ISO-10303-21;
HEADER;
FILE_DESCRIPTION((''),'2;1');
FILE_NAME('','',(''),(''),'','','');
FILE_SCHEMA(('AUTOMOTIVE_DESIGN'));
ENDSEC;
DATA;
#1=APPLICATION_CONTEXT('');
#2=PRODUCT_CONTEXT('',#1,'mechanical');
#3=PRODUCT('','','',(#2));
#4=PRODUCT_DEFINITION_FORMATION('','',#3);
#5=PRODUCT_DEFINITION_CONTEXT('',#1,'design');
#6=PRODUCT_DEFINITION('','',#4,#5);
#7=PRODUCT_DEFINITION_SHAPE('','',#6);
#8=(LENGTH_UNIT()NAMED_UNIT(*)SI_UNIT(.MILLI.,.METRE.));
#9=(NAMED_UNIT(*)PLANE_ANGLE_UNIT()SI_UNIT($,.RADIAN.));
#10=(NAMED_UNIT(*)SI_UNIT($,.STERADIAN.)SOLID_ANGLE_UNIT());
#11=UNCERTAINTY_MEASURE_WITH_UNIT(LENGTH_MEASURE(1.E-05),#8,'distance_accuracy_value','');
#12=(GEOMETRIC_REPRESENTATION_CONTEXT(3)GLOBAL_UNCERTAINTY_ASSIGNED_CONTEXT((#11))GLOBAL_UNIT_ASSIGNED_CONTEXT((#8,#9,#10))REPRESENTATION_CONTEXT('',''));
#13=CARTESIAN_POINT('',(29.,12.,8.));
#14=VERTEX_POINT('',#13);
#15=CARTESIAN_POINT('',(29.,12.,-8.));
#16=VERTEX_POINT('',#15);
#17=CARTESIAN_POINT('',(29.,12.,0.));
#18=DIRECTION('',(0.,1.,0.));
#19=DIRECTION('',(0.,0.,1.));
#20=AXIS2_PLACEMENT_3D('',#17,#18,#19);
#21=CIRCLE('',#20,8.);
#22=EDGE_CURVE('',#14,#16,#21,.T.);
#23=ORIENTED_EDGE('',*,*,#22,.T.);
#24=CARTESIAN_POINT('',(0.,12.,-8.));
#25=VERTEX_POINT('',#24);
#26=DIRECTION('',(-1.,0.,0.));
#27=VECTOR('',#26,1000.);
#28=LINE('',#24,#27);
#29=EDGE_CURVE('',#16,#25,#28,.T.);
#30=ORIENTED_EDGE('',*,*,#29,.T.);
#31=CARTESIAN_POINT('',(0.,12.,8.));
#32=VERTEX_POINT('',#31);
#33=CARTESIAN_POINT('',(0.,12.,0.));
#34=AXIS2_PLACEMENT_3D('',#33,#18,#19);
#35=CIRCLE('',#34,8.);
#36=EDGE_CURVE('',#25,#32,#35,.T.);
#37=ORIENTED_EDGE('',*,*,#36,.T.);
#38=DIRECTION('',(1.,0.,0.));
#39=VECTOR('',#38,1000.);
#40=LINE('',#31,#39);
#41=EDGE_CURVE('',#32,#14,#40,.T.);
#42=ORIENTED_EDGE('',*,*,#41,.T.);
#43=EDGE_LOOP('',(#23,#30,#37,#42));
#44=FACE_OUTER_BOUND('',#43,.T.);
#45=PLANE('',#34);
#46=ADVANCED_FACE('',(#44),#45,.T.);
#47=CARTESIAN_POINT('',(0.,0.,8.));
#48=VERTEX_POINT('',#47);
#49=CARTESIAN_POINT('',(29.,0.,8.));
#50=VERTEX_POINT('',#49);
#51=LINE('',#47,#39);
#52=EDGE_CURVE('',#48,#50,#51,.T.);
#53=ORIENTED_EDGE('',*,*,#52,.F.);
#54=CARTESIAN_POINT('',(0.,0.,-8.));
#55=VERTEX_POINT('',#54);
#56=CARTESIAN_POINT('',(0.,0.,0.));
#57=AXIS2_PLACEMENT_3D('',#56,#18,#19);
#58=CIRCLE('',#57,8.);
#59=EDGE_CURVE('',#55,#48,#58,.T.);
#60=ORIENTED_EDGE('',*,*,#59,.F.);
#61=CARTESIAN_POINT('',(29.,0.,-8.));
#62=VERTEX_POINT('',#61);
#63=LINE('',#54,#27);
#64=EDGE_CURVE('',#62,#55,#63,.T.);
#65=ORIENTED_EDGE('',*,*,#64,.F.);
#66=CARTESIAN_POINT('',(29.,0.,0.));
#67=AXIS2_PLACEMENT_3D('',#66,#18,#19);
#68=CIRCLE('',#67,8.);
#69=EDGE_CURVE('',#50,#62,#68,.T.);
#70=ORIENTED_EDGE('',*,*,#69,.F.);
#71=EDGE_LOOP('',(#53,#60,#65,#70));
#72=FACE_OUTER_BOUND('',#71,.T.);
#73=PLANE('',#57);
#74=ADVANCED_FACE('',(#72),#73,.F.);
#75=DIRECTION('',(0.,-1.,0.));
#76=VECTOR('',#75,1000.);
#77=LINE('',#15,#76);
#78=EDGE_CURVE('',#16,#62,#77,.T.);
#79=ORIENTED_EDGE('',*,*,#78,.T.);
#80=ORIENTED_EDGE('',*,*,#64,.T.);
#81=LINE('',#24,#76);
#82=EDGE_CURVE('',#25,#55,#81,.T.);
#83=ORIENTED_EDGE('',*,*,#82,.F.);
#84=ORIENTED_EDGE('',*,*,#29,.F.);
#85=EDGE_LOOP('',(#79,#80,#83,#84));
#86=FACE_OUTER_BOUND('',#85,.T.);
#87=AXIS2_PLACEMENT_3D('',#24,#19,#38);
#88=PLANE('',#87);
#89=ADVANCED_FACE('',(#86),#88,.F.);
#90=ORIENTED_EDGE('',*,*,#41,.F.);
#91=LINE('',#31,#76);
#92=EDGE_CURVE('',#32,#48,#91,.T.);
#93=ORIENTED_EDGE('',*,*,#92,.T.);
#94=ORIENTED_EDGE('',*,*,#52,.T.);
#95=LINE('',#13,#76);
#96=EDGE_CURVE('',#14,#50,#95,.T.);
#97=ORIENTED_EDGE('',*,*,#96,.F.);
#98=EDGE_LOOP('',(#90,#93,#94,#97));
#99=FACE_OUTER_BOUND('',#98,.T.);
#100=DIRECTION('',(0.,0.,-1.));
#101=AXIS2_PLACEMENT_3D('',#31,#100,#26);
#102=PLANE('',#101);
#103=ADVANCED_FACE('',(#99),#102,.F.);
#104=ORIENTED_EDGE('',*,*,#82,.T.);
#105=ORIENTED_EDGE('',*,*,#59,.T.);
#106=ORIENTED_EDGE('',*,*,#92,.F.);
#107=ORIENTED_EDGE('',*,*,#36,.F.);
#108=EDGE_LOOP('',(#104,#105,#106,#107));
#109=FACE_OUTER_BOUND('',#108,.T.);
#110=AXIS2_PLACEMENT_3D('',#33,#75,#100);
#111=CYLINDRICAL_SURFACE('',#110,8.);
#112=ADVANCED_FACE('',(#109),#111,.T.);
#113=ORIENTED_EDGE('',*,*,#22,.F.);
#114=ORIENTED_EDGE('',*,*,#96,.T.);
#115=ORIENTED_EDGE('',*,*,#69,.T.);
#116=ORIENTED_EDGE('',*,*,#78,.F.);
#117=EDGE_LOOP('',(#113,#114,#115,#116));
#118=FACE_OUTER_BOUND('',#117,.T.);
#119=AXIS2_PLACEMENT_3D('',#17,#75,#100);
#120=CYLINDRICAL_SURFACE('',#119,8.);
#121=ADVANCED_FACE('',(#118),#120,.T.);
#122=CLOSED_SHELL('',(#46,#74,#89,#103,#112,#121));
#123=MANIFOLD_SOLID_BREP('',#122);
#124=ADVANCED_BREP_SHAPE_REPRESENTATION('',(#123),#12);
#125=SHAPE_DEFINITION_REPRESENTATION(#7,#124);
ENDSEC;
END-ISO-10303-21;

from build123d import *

# Parameters (mm, degrees)
BOSS_EXTRUDE1_DEPTH = 12


with BuildPart() as part:
    # Sketch1 → Boss-Extrude1 (new body)
    with BuildSketch(Plane(origin=(0, 0, 0), x_dir=(1, 0, 0), z_dir=(0, 1, 0))):
        with BuildLine():
            Line((0, 8), (29, 8))
            ThreePointArc((29, 8), (37, 0), (29, -8))
            Line((29, -8), (0, -8))
            ThreePointArc((0, -8), (-8, 0), (0, 8))
        make_face()
    extrude(amount=BOSS_EXTRUDE1_DEPTH)


solid = part.part
